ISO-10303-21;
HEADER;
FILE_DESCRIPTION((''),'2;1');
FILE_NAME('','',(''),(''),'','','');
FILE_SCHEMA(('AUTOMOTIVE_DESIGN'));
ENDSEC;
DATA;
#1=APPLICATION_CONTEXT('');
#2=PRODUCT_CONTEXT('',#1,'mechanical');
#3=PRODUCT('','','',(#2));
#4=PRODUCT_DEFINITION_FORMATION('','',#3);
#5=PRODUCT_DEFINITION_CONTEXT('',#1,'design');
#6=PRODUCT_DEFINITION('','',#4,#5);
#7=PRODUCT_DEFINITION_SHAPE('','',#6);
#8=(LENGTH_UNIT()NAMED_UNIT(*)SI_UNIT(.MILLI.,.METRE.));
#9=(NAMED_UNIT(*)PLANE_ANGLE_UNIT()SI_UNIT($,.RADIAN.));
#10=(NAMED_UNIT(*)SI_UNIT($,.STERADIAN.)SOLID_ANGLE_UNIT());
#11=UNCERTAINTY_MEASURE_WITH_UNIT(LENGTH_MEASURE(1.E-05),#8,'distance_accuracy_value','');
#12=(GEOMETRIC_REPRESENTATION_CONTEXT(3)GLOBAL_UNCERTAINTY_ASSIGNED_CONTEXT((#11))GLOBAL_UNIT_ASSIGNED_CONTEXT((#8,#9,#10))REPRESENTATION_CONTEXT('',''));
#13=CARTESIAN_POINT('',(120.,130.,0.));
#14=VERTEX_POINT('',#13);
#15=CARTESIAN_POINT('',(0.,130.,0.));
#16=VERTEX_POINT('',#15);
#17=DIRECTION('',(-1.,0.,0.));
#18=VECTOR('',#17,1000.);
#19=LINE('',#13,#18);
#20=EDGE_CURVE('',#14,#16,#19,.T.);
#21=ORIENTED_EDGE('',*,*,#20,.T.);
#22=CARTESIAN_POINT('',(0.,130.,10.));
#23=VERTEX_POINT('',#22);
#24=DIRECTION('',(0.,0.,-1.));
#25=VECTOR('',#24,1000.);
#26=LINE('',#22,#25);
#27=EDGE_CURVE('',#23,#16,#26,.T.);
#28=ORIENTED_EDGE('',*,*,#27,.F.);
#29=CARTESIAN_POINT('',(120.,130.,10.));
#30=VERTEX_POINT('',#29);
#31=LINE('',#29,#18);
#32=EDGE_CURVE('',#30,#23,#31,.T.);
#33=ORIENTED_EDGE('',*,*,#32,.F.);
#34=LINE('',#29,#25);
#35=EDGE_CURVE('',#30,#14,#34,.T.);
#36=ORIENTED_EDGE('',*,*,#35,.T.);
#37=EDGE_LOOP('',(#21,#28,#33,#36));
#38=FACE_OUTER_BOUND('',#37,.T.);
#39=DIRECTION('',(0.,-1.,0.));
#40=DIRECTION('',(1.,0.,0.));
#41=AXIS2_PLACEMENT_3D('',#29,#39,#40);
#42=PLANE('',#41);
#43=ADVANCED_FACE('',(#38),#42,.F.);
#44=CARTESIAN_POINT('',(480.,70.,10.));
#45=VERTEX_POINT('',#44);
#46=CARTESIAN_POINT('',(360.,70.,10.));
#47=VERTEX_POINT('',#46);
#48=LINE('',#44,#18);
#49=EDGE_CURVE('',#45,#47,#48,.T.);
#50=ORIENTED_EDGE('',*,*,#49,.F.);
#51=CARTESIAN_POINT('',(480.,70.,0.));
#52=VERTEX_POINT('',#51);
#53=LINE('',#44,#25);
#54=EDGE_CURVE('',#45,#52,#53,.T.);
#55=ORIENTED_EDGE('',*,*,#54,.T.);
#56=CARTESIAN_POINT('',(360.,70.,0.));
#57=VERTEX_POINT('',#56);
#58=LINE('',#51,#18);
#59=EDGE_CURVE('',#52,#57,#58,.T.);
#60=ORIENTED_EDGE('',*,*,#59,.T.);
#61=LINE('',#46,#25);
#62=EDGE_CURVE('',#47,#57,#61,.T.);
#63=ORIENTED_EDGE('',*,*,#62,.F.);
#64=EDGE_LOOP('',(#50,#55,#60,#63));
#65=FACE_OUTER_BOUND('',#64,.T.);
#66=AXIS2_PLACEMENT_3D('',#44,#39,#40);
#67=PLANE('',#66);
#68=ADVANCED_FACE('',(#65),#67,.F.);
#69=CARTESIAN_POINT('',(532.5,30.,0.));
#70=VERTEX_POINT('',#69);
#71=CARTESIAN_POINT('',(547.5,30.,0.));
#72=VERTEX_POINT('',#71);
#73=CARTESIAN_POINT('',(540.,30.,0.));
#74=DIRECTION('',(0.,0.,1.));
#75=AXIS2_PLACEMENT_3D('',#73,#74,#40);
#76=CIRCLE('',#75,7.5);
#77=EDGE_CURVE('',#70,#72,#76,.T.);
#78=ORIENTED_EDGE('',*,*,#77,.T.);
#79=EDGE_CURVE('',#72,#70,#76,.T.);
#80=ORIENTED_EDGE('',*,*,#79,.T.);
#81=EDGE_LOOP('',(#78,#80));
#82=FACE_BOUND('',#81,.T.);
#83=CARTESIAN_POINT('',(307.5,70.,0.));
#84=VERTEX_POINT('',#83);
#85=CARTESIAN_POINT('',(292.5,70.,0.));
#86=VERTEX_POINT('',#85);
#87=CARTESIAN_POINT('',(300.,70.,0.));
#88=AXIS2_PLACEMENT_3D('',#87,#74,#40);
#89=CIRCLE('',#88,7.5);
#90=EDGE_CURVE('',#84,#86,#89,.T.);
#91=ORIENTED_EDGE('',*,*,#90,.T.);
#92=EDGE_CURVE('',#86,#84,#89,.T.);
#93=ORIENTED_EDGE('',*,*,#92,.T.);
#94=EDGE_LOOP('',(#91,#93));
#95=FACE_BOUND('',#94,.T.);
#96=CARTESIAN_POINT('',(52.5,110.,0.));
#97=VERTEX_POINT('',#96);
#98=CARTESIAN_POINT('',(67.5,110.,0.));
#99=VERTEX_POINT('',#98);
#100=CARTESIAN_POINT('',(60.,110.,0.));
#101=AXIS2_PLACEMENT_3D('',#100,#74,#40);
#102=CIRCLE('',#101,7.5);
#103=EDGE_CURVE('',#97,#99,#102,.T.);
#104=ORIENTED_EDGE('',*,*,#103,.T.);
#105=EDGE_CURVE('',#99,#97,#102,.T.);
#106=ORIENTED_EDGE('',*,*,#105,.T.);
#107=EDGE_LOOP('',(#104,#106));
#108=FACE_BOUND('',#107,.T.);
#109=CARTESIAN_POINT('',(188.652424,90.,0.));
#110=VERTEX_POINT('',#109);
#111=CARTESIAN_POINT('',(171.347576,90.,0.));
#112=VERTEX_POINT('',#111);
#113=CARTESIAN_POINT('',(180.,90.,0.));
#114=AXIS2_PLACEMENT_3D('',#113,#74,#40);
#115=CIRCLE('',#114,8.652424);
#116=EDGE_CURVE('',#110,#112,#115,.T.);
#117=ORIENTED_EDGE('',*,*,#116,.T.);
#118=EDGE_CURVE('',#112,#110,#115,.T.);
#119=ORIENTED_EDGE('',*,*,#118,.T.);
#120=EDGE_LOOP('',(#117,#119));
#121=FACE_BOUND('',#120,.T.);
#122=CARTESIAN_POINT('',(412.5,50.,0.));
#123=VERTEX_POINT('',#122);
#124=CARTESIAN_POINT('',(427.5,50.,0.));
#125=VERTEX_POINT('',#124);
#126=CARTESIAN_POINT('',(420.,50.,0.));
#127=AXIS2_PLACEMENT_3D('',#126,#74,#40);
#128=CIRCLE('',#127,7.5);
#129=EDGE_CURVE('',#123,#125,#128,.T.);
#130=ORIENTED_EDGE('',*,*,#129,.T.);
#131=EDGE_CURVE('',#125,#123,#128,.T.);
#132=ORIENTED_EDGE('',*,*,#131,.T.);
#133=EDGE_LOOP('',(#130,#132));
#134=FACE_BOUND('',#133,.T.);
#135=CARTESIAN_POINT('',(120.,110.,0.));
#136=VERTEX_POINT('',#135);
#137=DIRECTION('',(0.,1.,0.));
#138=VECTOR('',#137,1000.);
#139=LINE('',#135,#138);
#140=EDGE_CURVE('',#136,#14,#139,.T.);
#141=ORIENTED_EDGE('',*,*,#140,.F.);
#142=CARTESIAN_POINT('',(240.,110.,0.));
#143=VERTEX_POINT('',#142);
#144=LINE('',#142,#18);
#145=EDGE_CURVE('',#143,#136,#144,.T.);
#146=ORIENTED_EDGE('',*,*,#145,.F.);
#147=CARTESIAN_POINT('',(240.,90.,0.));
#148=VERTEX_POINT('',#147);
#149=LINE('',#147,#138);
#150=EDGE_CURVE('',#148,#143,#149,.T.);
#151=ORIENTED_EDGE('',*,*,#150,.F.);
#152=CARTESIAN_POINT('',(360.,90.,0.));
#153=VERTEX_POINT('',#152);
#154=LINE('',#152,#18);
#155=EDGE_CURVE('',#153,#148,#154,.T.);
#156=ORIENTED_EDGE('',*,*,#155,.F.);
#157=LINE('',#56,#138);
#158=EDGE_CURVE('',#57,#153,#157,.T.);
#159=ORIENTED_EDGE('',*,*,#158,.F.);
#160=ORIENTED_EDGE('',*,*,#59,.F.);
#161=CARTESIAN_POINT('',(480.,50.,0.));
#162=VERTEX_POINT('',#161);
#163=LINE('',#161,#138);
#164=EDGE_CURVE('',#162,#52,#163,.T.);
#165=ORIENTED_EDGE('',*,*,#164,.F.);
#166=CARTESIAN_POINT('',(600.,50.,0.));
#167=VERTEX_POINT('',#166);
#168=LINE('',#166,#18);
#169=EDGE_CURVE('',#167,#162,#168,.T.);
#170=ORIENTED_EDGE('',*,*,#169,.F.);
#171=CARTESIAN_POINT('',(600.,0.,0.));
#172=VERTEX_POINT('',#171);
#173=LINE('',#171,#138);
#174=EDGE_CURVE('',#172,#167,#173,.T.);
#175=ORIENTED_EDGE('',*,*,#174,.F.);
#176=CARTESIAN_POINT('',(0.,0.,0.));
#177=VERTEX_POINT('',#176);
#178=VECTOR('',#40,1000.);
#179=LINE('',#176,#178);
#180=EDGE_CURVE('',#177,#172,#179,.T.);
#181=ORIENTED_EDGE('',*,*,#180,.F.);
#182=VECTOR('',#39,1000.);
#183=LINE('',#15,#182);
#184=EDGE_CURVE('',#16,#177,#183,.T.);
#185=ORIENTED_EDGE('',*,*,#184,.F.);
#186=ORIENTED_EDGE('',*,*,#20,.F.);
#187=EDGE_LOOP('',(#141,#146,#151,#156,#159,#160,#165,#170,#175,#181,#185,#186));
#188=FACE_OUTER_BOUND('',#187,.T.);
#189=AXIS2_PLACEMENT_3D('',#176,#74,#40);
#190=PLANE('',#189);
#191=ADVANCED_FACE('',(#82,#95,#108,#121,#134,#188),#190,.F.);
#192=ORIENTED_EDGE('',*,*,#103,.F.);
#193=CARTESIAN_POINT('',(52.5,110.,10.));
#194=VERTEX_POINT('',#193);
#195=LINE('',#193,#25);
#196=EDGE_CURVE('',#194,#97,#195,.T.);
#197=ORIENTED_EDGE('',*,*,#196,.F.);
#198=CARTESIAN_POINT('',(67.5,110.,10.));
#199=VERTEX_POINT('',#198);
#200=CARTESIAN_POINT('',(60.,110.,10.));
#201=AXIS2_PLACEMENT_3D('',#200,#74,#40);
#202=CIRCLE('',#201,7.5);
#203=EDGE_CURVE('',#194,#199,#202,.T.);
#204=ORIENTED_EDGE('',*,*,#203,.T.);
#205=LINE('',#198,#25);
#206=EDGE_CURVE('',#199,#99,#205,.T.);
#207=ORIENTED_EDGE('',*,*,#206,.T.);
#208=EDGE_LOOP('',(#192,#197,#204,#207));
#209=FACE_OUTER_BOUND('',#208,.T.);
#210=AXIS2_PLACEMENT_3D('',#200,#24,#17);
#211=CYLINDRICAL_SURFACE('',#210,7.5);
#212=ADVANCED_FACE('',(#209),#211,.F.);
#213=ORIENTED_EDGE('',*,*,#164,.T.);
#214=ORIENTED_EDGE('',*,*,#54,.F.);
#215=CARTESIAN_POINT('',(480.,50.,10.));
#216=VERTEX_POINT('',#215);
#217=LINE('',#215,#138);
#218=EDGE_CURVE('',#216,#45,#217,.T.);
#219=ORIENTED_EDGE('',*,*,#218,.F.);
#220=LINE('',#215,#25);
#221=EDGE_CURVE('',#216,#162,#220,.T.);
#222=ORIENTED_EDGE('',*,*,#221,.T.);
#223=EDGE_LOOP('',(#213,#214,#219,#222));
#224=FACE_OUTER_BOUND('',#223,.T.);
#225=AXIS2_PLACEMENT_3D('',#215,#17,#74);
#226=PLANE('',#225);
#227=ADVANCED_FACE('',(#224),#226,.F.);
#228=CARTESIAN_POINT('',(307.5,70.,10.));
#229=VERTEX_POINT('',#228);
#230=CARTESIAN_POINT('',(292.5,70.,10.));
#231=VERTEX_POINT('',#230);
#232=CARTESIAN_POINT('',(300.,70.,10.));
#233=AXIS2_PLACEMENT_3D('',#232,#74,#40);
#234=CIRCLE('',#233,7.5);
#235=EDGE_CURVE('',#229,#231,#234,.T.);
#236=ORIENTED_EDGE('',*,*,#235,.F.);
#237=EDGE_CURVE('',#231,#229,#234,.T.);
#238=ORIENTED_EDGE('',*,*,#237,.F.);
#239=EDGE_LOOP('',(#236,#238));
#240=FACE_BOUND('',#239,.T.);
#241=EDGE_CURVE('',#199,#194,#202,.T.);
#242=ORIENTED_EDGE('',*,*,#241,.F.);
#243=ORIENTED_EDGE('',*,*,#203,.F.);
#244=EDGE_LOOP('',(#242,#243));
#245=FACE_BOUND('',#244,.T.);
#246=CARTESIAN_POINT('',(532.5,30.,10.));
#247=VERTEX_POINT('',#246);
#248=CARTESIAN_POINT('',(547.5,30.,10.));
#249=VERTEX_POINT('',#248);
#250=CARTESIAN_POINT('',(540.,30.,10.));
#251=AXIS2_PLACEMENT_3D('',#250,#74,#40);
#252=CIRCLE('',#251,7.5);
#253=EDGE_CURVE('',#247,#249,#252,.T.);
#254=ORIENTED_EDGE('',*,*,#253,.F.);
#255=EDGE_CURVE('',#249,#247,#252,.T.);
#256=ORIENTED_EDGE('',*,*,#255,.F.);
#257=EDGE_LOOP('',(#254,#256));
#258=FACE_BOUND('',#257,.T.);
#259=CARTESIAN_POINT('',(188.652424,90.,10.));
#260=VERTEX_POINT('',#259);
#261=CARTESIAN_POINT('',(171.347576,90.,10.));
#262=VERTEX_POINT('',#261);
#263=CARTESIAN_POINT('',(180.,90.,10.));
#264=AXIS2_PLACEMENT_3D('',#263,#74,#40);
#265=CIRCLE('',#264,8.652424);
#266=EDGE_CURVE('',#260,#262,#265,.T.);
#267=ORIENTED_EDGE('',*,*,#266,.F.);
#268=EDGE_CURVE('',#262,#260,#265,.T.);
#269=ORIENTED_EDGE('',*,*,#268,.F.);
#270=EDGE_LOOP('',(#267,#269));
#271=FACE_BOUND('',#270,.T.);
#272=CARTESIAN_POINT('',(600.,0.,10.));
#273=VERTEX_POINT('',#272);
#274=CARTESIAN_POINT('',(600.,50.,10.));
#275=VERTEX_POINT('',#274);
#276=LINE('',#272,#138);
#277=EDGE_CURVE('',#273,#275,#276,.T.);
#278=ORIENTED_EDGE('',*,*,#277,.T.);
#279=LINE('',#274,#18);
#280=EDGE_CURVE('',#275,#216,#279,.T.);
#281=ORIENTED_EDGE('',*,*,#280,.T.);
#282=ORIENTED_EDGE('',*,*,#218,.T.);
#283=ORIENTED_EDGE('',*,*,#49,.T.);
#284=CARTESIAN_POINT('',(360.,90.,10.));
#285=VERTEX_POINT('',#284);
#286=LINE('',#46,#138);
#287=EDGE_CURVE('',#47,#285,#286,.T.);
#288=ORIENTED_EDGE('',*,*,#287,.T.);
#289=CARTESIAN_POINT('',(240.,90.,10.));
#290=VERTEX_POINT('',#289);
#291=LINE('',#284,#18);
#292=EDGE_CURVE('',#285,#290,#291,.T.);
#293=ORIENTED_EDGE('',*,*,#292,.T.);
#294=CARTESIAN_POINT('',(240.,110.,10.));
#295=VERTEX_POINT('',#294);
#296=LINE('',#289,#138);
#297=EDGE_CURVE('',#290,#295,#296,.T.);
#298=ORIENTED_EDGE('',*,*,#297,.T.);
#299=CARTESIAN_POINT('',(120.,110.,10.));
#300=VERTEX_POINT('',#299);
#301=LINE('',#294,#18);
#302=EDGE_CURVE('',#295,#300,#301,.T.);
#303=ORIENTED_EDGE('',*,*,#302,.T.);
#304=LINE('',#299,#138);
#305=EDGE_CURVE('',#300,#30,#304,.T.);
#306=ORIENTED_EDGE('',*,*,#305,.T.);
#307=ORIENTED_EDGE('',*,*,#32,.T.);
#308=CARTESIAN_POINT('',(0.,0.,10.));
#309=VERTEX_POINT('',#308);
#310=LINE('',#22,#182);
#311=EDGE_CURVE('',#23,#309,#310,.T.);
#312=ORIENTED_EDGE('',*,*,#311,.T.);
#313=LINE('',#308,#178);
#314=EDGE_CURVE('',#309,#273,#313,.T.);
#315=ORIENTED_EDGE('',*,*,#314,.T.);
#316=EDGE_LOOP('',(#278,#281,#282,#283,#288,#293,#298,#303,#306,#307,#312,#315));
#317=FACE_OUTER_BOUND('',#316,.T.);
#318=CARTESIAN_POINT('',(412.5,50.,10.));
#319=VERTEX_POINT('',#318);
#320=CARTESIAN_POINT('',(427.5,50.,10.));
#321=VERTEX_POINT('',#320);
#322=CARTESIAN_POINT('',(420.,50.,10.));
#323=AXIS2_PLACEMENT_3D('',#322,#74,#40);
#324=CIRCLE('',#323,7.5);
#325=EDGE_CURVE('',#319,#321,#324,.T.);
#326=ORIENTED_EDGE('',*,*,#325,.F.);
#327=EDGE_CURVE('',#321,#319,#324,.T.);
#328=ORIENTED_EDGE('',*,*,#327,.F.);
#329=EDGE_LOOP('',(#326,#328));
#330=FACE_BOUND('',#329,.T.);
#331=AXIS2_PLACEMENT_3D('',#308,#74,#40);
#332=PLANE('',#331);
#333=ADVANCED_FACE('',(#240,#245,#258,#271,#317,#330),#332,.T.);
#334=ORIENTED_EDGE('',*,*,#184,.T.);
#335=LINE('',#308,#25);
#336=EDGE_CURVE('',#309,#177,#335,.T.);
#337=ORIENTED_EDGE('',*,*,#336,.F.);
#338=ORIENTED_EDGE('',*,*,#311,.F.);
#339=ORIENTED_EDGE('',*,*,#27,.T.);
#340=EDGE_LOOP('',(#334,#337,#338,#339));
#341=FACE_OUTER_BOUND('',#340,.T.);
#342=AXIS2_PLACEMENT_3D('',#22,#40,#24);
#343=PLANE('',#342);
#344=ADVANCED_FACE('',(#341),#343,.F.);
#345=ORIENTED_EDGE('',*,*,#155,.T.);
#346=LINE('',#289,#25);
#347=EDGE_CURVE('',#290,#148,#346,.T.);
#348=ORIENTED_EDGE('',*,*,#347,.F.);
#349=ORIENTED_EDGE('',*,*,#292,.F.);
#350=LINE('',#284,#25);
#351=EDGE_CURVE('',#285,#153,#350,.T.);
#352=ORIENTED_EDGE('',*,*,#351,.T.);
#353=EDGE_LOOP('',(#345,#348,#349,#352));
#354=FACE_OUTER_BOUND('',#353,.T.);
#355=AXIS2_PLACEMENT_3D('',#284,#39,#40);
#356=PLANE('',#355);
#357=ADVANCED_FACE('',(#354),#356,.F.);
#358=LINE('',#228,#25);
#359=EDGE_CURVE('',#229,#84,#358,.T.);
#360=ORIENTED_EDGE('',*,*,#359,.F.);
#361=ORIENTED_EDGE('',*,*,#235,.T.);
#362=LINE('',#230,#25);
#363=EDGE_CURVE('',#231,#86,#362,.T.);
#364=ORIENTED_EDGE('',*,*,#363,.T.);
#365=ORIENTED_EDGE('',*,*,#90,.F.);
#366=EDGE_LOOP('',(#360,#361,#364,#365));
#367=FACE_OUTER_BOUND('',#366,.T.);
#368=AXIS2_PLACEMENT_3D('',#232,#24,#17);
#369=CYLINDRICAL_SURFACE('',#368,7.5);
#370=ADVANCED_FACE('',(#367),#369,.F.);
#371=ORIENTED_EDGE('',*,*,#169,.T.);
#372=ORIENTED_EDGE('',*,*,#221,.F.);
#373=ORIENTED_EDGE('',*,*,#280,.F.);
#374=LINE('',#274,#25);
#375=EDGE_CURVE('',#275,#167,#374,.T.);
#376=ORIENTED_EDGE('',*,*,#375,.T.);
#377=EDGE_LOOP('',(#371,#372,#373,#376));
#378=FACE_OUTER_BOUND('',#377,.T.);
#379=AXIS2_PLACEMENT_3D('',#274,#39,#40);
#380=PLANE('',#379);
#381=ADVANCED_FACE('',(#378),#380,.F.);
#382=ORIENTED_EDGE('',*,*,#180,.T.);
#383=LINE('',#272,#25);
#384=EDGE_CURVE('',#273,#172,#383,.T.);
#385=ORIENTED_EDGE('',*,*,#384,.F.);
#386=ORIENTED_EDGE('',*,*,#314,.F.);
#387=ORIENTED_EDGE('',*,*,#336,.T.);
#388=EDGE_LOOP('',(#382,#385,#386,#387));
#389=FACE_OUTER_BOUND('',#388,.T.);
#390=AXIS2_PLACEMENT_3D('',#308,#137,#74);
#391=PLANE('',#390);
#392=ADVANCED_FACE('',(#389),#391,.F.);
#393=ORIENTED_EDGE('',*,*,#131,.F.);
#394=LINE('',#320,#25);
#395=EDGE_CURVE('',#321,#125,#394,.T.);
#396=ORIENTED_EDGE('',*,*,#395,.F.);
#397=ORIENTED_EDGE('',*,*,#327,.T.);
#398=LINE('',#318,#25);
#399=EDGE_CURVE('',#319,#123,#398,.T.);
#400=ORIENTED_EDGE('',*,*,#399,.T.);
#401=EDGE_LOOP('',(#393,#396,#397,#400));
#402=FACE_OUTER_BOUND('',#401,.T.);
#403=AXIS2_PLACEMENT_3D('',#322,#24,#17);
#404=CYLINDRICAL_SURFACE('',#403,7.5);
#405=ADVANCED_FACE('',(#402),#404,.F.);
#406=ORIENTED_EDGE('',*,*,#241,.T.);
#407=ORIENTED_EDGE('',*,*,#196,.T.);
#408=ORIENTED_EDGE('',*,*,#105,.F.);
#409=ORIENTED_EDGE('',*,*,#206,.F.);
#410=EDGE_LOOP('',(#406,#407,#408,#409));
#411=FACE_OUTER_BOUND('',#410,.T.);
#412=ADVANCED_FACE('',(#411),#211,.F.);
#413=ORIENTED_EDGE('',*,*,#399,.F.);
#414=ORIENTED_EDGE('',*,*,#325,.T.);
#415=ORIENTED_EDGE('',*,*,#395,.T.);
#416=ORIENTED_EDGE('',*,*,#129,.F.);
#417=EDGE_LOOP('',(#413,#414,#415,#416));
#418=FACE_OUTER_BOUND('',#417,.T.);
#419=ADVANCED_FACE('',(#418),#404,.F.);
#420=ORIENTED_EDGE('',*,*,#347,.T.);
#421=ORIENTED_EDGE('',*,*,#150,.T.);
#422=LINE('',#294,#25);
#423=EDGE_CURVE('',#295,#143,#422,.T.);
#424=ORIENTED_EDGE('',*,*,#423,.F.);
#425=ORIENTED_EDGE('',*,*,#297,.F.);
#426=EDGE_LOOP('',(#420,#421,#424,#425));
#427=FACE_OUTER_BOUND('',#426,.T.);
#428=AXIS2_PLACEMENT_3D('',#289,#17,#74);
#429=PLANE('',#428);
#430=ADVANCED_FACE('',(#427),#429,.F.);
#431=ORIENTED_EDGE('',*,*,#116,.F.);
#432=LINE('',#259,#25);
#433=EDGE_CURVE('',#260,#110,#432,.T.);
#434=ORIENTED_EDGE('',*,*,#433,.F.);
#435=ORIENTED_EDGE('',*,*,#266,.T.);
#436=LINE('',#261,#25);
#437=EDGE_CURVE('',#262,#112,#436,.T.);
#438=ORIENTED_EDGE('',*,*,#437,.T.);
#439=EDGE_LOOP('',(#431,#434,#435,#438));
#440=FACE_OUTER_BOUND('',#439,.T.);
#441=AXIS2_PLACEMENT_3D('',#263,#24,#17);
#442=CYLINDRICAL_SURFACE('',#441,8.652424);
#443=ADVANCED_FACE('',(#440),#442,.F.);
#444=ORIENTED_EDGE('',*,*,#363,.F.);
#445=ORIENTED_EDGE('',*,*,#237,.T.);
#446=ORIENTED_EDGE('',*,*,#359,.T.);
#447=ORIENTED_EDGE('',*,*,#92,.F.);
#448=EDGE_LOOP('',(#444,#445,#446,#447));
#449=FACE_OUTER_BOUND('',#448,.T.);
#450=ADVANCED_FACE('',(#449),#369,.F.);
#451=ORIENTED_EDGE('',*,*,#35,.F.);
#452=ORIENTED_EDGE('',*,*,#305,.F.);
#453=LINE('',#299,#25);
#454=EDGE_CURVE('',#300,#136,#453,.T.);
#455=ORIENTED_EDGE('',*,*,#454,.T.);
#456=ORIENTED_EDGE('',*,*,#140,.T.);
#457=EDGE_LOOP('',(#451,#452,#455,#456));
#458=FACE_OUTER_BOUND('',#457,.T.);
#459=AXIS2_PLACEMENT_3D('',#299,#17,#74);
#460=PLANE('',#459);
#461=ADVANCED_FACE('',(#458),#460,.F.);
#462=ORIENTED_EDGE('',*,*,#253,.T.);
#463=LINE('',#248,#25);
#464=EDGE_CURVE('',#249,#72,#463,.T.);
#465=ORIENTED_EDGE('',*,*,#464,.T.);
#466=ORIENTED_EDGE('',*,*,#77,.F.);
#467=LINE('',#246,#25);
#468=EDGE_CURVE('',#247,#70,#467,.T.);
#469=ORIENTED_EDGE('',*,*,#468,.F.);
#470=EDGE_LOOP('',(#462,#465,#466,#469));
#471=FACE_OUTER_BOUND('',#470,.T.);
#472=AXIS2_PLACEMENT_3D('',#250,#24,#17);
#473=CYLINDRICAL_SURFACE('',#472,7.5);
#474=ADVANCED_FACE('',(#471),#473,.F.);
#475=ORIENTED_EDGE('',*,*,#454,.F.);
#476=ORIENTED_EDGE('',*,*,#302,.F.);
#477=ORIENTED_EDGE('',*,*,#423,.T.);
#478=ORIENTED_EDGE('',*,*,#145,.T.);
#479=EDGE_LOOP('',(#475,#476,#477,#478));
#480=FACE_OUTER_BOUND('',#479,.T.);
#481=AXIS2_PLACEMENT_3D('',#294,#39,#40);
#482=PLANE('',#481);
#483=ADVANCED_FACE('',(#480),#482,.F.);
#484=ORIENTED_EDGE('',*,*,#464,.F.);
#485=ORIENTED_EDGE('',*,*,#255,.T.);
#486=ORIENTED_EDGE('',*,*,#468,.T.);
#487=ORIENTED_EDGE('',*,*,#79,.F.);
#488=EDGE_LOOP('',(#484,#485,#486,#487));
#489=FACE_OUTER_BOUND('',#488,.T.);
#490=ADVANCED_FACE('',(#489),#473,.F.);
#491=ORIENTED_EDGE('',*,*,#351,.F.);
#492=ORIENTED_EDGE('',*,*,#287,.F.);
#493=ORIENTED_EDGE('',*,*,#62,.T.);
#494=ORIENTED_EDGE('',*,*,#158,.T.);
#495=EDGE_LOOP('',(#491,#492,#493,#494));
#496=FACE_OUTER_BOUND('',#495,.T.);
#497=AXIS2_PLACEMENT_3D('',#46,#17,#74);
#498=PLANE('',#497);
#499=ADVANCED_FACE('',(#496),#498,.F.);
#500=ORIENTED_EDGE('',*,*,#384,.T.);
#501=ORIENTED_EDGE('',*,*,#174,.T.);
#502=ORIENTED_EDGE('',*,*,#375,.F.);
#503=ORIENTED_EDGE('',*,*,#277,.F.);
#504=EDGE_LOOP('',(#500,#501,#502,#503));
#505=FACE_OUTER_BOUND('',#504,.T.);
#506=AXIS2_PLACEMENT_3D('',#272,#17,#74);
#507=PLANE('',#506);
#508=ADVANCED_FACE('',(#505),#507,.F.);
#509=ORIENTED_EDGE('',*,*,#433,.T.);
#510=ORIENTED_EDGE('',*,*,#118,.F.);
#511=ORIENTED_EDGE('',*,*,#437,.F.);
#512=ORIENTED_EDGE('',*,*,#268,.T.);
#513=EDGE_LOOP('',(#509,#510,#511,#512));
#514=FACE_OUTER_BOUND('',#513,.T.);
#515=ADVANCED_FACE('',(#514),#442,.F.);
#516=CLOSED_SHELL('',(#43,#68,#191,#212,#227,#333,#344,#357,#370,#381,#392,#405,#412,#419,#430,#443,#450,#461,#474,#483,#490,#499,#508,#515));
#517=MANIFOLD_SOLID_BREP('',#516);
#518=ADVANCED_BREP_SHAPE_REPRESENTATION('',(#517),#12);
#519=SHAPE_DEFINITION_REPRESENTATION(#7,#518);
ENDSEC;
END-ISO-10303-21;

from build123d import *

# Parameters (mm, degrees)
SKETCH1_R           = 7.5
SKETCH1_R_2         = 8.652423936
BOSS_EXTRUDE1_DEPTH = 10


with BuildPart() as part:
    # Sketch1 → Boss-Extrude1 (new body)
    with BuildSketch(Plane.XY):
        Polygon((0, 0), (600, 0), (600, 50), (480, 50), (480, 70), (360, 70), (360, 90), (240, 90), (240, 110), (120, 110), (120, 130), (0, 130), align=None)
        with Locations((60, 110)):
            Circle(SKETCH1_R, mode=Mode.SUBTRACT)
        with Locations((180, 90)):
            Circle(SKETCH1_R_2, mode=Mode.SUBTRACT)
        with Locations((300, 70)):
            Circle(SKETCH1_R, mode=Mode.SUBTRACT)
        with Locations((420, 50)):
            Circle(SKETCH1_R, mode=Mode.SUBTRACT)
        with Locations((540, 30)):
            Circle(SKETCH1_R, mode=Mode.SUBTRACT)
    extrude(amount=BOSS_EXTRUDE1_DEPTH)


solid = part.part
